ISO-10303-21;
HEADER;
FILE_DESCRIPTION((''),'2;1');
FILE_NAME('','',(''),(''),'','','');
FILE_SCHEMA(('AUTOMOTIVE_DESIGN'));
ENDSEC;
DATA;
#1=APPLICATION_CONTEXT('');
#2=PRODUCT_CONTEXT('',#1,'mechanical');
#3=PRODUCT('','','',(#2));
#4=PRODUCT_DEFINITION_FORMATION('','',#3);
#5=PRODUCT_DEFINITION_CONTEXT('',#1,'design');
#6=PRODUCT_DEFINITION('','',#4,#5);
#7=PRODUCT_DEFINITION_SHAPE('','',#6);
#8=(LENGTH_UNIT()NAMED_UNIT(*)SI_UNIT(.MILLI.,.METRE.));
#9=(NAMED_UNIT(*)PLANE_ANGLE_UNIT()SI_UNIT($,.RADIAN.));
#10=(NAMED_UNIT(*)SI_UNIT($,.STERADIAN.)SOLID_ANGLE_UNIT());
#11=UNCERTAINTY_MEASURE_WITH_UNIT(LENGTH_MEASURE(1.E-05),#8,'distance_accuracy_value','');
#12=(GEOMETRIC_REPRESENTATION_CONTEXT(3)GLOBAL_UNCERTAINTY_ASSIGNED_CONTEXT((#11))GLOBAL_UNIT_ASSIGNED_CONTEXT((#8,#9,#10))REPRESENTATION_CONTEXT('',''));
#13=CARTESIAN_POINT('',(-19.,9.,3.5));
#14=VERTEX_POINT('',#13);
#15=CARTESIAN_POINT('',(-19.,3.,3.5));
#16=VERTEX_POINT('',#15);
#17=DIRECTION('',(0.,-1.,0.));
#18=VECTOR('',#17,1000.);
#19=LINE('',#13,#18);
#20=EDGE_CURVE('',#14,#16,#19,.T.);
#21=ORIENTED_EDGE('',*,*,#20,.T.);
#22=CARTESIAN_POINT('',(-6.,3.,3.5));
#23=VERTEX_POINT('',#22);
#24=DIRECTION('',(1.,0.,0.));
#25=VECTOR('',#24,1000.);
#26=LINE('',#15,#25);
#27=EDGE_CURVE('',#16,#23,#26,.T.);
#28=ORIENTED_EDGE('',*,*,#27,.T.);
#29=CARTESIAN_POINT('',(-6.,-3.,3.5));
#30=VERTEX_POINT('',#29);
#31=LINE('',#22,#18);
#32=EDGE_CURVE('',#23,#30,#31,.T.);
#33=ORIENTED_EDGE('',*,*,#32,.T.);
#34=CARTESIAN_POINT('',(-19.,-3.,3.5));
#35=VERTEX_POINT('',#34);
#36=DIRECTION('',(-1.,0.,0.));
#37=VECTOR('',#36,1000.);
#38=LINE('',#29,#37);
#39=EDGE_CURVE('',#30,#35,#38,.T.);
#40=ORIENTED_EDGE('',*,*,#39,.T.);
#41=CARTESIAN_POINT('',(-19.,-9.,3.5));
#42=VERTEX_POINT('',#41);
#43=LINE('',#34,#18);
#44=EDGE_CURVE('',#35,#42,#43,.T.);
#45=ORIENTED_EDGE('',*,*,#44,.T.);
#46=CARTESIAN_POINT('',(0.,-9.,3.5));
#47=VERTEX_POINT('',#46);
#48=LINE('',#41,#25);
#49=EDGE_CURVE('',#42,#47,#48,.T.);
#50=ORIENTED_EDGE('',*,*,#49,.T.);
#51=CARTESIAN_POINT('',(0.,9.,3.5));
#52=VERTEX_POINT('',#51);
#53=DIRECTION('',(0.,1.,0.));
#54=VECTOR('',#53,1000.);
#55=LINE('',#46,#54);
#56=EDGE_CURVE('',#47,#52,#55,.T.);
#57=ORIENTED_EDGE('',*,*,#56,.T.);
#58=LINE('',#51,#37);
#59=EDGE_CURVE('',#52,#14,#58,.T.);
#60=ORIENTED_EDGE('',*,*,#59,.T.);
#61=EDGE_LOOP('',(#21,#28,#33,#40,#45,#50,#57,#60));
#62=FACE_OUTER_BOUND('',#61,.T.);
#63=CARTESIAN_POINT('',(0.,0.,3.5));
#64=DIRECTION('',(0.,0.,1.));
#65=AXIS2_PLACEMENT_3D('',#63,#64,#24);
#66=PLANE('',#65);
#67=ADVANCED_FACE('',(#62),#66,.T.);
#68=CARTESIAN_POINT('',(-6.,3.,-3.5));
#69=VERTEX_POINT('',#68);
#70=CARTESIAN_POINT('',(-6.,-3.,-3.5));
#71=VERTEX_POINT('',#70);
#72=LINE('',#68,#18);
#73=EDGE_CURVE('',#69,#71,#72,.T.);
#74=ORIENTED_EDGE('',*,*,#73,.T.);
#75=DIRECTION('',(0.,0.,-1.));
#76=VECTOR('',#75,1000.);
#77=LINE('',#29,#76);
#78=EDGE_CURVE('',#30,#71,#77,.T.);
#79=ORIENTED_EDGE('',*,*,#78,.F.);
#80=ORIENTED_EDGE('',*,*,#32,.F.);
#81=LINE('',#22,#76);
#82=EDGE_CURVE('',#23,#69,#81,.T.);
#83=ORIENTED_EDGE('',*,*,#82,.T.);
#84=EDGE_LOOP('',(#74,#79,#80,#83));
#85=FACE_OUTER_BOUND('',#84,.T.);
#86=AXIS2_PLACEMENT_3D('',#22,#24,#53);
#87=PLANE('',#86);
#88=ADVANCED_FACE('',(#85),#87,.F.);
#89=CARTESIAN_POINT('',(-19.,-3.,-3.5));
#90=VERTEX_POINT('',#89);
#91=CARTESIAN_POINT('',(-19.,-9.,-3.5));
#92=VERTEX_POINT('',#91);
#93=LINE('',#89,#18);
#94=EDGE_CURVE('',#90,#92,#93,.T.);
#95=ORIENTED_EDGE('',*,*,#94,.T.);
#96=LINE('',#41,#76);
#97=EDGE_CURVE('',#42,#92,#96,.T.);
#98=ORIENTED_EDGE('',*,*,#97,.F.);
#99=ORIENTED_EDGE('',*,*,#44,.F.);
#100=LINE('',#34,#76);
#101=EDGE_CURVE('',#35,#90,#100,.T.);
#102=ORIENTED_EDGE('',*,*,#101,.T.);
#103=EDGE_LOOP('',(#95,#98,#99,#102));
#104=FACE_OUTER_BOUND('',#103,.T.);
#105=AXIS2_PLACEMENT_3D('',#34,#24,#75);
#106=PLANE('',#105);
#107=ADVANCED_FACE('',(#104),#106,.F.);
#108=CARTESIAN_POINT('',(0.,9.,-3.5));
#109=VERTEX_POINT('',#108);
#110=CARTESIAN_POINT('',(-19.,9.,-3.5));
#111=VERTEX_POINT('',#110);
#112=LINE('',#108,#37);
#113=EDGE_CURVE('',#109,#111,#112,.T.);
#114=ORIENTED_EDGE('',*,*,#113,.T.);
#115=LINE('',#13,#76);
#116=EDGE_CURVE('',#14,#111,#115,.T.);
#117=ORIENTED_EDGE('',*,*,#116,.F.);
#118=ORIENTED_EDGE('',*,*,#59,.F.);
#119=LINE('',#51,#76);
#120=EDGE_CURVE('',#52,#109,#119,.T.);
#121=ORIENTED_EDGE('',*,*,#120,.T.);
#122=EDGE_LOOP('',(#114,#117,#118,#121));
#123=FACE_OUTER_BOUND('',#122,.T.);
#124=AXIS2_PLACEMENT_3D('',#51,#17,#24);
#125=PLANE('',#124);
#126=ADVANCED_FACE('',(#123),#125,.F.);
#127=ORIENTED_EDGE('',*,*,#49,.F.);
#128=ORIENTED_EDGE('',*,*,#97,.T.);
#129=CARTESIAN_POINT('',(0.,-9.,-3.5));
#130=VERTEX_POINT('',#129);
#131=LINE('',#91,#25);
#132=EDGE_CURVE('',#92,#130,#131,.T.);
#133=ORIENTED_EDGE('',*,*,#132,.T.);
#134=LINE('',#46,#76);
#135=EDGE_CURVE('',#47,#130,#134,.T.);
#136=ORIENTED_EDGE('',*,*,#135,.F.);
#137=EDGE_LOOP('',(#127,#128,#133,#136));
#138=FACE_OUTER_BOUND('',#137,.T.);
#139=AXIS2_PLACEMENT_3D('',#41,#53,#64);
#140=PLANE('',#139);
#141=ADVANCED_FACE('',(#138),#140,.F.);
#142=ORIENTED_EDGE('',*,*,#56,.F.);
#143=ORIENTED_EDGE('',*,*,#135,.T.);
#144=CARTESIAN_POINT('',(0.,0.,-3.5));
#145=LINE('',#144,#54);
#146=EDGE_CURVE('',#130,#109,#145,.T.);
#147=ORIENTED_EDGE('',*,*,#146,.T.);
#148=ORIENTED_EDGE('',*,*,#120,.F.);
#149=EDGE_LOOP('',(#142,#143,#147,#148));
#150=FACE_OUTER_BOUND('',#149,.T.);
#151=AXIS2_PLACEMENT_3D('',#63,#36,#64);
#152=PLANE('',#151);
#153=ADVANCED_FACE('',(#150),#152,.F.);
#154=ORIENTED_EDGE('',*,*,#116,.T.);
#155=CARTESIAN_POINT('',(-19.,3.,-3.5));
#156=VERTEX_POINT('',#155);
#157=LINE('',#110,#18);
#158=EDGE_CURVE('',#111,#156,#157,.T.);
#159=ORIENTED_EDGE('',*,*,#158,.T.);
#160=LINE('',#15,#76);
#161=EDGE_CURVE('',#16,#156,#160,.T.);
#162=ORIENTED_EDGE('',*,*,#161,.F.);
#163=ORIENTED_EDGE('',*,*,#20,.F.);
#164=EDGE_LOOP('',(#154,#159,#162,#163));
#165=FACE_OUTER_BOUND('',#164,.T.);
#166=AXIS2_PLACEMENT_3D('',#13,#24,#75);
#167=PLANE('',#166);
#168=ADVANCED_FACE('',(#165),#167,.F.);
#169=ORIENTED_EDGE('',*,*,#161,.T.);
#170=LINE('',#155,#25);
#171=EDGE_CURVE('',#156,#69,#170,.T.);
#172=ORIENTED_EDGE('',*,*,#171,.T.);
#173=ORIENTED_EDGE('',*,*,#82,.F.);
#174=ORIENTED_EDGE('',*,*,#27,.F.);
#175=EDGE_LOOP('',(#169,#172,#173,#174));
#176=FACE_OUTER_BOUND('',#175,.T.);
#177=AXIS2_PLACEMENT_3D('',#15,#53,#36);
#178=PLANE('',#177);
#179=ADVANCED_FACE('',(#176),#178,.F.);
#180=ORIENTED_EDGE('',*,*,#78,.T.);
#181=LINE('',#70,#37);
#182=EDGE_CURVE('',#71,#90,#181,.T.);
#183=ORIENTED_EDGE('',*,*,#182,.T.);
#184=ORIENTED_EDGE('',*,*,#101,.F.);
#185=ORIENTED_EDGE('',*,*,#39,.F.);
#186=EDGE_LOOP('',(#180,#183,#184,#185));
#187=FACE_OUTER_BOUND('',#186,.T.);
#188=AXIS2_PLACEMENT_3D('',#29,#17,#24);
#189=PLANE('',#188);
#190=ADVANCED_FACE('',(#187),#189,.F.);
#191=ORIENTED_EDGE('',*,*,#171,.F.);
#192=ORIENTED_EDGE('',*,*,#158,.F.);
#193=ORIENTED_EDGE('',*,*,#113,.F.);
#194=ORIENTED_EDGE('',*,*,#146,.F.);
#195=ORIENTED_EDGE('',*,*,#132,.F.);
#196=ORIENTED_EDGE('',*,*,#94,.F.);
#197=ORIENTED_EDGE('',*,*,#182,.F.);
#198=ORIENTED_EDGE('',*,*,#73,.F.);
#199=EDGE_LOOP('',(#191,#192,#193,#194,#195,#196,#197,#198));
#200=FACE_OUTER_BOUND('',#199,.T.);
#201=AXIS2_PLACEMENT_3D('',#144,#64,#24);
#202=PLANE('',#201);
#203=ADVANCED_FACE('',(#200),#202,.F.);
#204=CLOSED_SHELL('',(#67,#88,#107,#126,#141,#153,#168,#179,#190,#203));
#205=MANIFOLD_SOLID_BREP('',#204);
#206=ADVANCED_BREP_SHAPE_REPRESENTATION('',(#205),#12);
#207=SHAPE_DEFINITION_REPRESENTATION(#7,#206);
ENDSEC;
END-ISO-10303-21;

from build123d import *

# Parameters (mm, degrees)
EXTRUDE_1_DEPTH = 3.5


with BuildPart() as part:
    # 草图1 → 凸台-拉伸1 (new, symmetric)
    with BuildSketch(Plane.XY):
        Polygon((0, 0), (0, 9), (-19, 9), (-19, 3), (-6, 3), (-6, -3), (-19, -3), (-19, -9), (0, -9), align=None)
    extrude(amount=EXTRUDE_1_DEPTH, both=True)


solid = part.part
